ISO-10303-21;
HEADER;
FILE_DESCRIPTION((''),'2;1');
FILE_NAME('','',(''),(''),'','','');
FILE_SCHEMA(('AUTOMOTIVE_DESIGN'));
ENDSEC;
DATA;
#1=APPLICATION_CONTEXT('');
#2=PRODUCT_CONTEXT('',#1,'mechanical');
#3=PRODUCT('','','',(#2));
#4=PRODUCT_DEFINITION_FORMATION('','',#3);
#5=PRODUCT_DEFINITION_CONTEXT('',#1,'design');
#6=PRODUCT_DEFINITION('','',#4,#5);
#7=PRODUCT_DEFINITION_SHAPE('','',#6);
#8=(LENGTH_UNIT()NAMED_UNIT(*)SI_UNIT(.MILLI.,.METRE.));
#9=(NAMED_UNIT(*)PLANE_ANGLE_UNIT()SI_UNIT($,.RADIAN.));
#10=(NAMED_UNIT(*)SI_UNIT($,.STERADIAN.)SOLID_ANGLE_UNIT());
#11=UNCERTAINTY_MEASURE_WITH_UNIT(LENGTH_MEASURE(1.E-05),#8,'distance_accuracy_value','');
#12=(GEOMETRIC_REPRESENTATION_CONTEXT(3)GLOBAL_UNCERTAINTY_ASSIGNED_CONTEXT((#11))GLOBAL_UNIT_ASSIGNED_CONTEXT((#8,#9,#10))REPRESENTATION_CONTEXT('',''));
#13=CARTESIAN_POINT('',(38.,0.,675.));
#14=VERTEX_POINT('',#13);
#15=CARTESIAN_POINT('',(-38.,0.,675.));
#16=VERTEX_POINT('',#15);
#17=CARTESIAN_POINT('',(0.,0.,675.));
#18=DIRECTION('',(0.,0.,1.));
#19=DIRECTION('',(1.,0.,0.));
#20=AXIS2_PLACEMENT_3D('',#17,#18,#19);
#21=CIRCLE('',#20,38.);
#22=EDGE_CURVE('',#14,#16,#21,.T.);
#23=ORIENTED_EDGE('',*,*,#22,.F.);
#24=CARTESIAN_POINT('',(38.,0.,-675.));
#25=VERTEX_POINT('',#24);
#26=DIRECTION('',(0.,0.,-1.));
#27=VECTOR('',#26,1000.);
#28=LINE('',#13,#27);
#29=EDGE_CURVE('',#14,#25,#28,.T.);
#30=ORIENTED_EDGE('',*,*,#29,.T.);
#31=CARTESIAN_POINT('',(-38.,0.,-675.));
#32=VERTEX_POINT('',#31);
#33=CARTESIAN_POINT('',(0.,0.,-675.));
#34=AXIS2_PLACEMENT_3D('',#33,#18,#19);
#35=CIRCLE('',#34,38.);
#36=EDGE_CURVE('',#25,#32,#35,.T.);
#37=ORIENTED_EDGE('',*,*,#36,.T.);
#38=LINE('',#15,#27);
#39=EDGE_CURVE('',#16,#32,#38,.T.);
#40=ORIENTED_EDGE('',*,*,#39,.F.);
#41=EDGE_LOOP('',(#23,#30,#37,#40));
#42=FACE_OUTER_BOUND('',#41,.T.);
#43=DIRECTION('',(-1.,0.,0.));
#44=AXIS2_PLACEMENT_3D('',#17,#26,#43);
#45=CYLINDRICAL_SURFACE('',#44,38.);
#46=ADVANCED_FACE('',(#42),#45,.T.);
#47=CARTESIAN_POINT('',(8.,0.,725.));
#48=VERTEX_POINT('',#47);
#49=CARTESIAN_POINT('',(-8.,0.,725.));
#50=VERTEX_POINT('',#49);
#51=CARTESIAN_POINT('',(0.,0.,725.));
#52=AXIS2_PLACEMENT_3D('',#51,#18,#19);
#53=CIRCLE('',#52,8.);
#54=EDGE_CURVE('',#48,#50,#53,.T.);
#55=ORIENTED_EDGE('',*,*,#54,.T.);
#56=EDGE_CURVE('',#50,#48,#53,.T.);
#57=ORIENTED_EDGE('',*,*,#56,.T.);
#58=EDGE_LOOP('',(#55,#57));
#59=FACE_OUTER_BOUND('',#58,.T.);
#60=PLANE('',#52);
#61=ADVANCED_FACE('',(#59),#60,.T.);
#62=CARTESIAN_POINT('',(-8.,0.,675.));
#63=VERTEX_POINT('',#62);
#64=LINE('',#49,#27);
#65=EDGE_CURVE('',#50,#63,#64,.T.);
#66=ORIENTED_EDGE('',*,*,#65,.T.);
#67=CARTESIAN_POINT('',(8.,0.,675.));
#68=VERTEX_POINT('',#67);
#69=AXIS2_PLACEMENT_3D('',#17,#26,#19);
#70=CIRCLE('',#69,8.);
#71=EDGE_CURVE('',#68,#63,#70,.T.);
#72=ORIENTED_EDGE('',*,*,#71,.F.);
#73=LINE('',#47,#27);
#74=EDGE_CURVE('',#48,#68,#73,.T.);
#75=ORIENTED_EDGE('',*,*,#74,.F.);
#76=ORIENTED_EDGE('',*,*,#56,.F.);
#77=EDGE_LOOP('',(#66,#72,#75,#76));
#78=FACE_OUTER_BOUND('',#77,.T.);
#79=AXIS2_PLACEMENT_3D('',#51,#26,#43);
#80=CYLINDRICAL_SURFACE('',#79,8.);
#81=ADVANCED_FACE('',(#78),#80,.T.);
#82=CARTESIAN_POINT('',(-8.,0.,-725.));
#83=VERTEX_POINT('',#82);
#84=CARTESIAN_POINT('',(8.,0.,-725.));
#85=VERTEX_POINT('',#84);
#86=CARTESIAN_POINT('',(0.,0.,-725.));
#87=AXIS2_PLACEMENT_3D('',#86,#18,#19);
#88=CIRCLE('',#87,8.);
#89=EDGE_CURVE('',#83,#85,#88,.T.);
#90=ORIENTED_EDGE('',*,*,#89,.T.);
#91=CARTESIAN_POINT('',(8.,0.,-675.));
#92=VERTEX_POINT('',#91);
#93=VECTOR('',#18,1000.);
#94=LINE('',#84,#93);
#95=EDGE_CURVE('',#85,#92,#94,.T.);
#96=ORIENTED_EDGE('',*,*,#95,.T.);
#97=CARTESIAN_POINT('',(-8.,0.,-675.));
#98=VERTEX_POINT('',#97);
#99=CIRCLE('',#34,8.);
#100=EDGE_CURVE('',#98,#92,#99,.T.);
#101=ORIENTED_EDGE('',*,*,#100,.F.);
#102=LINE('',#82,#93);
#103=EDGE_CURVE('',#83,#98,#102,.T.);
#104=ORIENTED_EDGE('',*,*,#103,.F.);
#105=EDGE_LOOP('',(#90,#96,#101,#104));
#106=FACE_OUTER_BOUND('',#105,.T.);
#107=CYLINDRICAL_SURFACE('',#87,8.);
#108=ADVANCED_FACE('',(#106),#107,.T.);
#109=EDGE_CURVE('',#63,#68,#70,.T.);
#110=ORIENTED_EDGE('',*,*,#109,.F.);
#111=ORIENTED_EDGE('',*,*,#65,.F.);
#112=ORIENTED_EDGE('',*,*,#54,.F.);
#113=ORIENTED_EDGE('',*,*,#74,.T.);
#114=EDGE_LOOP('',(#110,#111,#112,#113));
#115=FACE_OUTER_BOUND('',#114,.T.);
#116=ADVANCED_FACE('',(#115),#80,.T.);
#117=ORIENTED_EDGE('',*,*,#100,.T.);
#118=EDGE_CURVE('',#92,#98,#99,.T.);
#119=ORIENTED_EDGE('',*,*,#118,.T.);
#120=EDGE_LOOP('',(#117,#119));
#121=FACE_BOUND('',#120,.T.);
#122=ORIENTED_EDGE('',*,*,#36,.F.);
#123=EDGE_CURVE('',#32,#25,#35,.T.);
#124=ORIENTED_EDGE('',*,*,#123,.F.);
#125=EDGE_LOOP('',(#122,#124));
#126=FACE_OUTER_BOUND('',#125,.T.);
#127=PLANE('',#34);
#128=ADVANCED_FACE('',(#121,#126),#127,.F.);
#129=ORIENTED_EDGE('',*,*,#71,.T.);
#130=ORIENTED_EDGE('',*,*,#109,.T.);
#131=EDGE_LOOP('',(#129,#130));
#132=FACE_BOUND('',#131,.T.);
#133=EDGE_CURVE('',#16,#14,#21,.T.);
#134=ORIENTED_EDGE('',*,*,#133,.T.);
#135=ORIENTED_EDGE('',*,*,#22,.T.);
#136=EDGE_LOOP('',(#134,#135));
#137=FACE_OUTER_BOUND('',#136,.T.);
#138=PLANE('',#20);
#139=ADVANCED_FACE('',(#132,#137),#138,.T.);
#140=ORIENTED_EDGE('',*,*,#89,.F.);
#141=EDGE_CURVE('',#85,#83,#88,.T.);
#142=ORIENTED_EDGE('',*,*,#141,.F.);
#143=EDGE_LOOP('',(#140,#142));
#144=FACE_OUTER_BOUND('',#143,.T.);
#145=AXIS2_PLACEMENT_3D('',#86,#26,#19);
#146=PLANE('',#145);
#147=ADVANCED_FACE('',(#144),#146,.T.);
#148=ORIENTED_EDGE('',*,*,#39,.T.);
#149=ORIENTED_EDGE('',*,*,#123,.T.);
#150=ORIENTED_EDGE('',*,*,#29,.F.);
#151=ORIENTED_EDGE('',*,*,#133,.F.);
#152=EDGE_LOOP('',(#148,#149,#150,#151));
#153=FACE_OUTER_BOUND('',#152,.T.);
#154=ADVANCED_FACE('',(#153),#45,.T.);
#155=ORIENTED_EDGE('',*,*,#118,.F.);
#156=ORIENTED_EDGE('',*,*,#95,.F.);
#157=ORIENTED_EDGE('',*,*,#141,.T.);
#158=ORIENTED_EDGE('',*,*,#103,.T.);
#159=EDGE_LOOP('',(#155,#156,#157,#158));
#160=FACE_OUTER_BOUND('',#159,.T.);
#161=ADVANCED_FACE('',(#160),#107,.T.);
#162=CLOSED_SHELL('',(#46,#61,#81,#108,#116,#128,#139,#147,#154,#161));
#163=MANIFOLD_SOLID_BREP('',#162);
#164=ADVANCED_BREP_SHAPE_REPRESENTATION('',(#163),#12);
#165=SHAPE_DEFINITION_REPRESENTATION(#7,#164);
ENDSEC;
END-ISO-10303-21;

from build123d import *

# Parameters (mm, degrees)
SKETCH_1_R      = 38
EXTRUDE_1_DEPTH = 675
SKETCH_2_R      = 8
EXTRUDE_2_DEPTH = 50


with BuildPart() as part:
    # 草图1 → 凸台-拉伸1 (new, symmetric)
    with BuildSketch(Plane.XY):
        Circle(SKETCH_1_R)
    extrude(amount=EXTRUDE_1_DEPTH, both=True)

    # 草图2 → 凸台-拉伸2 (add, symmetric)
    with BuildSketch(Plane.XY.offset(675)):
        Circle(SKETCH_2_R)
    extrude_2 = extrude(amount=EXTRUDE_2_DEPTH, both=True)

    # 镜向1: 凸台-拉伸2 across plane
    add(extrude_2.mirror(Plane.XY))


solid = part.part
